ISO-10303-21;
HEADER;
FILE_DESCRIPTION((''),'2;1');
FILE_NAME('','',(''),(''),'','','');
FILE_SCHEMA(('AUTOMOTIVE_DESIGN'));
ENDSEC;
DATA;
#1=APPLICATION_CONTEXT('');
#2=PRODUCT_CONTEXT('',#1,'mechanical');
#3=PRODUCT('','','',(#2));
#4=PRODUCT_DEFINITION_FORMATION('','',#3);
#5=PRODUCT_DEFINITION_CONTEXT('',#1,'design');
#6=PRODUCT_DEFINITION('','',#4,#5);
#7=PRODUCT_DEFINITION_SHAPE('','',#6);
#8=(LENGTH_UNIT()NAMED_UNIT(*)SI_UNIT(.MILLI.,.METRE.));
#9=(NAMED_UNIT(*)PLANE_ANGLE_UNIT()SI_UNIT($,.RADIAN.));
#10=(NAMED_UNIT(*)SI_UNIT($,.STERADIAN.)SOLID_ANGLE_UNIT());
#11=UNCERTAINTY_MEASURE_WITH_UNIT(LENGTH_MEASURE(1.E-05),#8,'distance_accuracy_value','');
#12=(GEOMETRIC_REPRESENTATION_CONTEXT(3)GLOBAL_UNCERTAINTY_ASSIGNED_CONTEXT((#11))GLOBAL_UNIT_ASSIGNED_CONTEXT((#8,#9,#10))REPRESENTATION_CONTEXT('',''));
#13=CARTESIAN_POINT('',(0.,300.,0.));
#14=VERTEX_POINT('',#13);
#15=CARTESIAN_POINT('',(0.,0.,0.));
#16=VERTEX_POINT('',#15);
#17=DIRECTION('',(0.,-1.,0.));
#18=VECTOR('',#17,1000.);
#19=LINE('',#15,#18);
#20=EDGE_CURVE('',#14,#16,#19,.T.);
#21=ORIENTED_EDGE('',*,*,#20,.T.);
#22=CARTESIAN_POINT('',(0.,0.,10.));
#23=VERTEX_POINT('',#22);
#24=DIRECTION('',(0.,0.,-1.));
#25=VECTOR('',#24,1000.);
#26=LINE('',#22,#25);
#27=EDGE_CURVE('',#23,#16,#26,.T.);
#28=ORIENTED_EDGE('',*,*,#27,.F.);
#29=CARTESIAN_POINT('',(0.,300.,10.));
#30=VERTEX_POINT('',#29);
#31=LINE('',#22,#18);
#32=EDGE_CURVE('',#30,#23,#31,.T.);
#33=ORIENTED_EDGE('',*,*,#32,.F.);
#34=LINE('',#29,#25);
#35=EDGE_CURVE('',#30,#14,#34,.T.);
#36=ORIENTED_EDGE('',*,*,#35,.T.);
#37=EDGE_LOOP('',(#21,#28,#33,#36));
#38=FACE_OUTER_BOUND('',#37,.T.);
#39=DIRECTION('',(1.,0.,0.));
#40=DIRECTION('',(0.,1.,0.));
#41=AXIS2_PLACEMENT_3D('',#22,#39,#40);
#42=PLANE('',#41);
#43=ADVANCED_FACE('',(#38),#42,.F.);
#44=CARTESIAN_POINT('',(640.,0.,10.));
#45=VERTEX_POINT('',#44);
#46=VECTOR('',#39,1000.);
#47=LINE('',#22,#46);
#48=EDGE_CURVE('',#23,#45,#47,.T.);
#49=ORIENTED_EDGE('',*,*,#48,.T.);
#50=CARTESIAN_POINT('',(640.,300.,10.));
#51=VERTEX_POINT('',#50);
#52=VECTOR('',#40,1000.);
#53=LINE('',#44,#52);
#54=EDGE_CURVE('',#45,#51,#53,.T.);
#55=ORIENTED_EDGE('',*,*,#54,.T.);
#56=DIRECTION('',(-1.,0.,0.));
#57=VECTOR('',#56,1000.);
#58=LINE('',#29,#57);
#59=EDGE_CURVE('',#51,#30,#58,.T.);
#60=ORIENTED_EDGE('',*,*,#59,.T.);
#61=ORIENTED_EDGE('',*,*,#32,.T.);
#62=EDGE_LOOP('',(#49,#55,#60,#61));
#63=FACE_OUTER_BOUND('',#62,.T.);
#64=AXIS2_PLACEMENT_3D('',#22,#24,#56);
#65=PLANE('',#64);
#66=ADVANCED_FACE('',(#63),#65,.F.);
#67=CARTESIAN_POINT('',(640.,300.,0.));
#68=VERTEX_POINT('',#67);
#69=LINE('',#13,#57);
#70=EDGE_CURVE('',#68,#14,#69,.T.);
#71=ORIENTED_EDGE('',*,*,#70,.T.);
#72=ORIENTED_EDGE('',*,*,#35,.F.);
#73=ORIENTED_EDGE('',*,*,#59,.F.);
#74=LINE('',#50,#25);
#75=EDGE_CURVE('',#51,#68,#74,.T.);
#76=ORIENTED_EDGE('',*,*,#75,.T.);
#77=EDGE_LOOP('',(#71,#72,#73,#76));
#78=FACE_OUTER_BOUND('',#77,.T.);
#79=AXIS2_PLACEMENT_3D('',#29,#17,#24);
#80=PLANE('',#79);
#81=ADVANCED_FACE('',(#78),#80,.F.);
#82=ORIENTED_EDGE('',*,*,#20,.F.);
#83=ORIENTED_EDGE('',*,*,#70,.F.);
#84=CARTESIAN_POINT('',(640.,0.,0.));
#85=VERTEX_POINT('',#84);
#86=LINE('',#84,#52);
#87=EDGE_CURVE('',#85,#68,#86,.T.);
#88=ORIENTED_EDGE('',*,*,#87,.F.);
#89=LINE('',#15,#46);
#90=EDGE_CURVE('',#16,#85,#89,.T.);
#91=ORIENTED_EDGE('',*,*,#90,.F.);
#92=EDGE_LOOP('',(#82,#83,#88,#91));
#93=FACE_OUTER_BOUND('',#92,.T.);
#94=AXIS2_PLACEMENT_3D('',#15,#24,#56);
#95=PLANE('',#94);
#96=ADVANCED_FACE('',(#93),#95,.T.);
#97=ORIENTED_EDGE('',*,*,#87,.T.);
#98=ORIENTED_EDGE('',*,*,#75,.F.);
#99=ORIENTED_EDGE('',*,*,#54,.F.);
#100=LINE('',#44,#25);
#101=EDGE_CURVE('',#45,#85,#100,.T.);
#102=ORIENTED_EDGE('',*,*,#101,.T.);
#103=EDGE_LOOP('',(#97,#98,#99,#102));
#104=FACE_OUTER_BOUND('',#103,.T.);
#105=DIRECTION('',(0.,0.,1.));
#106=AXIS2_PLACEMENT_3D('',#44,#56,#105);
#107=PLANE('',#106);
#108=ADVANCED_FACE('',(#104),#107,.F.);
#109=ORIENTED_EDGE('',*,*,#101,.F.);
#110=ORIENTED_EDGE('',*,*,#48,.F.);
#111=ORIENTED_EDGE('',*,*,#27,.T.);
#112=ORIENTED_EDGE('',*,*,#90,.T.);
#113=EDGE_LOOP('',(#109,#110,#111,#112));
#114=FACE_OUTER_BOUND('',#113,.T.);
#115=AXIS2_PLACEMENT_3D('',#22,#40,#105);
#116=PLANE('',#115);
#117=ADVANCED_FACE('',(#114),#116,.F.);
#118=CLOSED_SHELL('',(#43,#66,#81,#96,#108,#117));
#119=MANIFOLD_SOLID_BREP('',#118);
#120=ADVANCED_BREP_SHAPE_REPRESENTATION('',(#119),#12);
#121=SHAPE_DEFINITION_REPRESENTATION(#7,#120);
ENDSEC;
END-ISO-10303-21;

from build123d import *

# Parameters (mm, degrees)
SKETCH1_W           = 640
SKETCH1_H           = 300
BOSS_EXTRUDE1_DEPTH = 10


with BuildPart() as part:
    # Sketch1 → Boss-Extrude1 (new body)
    with BuildSketch(Plane.XY):
        with Locations((320, 150)):
            Rectangle(SKETCH1_W, SKETCH1_H)
    extrude(amount=BOSS_EXTRUDE1_DEPTH)


solid = part.part
